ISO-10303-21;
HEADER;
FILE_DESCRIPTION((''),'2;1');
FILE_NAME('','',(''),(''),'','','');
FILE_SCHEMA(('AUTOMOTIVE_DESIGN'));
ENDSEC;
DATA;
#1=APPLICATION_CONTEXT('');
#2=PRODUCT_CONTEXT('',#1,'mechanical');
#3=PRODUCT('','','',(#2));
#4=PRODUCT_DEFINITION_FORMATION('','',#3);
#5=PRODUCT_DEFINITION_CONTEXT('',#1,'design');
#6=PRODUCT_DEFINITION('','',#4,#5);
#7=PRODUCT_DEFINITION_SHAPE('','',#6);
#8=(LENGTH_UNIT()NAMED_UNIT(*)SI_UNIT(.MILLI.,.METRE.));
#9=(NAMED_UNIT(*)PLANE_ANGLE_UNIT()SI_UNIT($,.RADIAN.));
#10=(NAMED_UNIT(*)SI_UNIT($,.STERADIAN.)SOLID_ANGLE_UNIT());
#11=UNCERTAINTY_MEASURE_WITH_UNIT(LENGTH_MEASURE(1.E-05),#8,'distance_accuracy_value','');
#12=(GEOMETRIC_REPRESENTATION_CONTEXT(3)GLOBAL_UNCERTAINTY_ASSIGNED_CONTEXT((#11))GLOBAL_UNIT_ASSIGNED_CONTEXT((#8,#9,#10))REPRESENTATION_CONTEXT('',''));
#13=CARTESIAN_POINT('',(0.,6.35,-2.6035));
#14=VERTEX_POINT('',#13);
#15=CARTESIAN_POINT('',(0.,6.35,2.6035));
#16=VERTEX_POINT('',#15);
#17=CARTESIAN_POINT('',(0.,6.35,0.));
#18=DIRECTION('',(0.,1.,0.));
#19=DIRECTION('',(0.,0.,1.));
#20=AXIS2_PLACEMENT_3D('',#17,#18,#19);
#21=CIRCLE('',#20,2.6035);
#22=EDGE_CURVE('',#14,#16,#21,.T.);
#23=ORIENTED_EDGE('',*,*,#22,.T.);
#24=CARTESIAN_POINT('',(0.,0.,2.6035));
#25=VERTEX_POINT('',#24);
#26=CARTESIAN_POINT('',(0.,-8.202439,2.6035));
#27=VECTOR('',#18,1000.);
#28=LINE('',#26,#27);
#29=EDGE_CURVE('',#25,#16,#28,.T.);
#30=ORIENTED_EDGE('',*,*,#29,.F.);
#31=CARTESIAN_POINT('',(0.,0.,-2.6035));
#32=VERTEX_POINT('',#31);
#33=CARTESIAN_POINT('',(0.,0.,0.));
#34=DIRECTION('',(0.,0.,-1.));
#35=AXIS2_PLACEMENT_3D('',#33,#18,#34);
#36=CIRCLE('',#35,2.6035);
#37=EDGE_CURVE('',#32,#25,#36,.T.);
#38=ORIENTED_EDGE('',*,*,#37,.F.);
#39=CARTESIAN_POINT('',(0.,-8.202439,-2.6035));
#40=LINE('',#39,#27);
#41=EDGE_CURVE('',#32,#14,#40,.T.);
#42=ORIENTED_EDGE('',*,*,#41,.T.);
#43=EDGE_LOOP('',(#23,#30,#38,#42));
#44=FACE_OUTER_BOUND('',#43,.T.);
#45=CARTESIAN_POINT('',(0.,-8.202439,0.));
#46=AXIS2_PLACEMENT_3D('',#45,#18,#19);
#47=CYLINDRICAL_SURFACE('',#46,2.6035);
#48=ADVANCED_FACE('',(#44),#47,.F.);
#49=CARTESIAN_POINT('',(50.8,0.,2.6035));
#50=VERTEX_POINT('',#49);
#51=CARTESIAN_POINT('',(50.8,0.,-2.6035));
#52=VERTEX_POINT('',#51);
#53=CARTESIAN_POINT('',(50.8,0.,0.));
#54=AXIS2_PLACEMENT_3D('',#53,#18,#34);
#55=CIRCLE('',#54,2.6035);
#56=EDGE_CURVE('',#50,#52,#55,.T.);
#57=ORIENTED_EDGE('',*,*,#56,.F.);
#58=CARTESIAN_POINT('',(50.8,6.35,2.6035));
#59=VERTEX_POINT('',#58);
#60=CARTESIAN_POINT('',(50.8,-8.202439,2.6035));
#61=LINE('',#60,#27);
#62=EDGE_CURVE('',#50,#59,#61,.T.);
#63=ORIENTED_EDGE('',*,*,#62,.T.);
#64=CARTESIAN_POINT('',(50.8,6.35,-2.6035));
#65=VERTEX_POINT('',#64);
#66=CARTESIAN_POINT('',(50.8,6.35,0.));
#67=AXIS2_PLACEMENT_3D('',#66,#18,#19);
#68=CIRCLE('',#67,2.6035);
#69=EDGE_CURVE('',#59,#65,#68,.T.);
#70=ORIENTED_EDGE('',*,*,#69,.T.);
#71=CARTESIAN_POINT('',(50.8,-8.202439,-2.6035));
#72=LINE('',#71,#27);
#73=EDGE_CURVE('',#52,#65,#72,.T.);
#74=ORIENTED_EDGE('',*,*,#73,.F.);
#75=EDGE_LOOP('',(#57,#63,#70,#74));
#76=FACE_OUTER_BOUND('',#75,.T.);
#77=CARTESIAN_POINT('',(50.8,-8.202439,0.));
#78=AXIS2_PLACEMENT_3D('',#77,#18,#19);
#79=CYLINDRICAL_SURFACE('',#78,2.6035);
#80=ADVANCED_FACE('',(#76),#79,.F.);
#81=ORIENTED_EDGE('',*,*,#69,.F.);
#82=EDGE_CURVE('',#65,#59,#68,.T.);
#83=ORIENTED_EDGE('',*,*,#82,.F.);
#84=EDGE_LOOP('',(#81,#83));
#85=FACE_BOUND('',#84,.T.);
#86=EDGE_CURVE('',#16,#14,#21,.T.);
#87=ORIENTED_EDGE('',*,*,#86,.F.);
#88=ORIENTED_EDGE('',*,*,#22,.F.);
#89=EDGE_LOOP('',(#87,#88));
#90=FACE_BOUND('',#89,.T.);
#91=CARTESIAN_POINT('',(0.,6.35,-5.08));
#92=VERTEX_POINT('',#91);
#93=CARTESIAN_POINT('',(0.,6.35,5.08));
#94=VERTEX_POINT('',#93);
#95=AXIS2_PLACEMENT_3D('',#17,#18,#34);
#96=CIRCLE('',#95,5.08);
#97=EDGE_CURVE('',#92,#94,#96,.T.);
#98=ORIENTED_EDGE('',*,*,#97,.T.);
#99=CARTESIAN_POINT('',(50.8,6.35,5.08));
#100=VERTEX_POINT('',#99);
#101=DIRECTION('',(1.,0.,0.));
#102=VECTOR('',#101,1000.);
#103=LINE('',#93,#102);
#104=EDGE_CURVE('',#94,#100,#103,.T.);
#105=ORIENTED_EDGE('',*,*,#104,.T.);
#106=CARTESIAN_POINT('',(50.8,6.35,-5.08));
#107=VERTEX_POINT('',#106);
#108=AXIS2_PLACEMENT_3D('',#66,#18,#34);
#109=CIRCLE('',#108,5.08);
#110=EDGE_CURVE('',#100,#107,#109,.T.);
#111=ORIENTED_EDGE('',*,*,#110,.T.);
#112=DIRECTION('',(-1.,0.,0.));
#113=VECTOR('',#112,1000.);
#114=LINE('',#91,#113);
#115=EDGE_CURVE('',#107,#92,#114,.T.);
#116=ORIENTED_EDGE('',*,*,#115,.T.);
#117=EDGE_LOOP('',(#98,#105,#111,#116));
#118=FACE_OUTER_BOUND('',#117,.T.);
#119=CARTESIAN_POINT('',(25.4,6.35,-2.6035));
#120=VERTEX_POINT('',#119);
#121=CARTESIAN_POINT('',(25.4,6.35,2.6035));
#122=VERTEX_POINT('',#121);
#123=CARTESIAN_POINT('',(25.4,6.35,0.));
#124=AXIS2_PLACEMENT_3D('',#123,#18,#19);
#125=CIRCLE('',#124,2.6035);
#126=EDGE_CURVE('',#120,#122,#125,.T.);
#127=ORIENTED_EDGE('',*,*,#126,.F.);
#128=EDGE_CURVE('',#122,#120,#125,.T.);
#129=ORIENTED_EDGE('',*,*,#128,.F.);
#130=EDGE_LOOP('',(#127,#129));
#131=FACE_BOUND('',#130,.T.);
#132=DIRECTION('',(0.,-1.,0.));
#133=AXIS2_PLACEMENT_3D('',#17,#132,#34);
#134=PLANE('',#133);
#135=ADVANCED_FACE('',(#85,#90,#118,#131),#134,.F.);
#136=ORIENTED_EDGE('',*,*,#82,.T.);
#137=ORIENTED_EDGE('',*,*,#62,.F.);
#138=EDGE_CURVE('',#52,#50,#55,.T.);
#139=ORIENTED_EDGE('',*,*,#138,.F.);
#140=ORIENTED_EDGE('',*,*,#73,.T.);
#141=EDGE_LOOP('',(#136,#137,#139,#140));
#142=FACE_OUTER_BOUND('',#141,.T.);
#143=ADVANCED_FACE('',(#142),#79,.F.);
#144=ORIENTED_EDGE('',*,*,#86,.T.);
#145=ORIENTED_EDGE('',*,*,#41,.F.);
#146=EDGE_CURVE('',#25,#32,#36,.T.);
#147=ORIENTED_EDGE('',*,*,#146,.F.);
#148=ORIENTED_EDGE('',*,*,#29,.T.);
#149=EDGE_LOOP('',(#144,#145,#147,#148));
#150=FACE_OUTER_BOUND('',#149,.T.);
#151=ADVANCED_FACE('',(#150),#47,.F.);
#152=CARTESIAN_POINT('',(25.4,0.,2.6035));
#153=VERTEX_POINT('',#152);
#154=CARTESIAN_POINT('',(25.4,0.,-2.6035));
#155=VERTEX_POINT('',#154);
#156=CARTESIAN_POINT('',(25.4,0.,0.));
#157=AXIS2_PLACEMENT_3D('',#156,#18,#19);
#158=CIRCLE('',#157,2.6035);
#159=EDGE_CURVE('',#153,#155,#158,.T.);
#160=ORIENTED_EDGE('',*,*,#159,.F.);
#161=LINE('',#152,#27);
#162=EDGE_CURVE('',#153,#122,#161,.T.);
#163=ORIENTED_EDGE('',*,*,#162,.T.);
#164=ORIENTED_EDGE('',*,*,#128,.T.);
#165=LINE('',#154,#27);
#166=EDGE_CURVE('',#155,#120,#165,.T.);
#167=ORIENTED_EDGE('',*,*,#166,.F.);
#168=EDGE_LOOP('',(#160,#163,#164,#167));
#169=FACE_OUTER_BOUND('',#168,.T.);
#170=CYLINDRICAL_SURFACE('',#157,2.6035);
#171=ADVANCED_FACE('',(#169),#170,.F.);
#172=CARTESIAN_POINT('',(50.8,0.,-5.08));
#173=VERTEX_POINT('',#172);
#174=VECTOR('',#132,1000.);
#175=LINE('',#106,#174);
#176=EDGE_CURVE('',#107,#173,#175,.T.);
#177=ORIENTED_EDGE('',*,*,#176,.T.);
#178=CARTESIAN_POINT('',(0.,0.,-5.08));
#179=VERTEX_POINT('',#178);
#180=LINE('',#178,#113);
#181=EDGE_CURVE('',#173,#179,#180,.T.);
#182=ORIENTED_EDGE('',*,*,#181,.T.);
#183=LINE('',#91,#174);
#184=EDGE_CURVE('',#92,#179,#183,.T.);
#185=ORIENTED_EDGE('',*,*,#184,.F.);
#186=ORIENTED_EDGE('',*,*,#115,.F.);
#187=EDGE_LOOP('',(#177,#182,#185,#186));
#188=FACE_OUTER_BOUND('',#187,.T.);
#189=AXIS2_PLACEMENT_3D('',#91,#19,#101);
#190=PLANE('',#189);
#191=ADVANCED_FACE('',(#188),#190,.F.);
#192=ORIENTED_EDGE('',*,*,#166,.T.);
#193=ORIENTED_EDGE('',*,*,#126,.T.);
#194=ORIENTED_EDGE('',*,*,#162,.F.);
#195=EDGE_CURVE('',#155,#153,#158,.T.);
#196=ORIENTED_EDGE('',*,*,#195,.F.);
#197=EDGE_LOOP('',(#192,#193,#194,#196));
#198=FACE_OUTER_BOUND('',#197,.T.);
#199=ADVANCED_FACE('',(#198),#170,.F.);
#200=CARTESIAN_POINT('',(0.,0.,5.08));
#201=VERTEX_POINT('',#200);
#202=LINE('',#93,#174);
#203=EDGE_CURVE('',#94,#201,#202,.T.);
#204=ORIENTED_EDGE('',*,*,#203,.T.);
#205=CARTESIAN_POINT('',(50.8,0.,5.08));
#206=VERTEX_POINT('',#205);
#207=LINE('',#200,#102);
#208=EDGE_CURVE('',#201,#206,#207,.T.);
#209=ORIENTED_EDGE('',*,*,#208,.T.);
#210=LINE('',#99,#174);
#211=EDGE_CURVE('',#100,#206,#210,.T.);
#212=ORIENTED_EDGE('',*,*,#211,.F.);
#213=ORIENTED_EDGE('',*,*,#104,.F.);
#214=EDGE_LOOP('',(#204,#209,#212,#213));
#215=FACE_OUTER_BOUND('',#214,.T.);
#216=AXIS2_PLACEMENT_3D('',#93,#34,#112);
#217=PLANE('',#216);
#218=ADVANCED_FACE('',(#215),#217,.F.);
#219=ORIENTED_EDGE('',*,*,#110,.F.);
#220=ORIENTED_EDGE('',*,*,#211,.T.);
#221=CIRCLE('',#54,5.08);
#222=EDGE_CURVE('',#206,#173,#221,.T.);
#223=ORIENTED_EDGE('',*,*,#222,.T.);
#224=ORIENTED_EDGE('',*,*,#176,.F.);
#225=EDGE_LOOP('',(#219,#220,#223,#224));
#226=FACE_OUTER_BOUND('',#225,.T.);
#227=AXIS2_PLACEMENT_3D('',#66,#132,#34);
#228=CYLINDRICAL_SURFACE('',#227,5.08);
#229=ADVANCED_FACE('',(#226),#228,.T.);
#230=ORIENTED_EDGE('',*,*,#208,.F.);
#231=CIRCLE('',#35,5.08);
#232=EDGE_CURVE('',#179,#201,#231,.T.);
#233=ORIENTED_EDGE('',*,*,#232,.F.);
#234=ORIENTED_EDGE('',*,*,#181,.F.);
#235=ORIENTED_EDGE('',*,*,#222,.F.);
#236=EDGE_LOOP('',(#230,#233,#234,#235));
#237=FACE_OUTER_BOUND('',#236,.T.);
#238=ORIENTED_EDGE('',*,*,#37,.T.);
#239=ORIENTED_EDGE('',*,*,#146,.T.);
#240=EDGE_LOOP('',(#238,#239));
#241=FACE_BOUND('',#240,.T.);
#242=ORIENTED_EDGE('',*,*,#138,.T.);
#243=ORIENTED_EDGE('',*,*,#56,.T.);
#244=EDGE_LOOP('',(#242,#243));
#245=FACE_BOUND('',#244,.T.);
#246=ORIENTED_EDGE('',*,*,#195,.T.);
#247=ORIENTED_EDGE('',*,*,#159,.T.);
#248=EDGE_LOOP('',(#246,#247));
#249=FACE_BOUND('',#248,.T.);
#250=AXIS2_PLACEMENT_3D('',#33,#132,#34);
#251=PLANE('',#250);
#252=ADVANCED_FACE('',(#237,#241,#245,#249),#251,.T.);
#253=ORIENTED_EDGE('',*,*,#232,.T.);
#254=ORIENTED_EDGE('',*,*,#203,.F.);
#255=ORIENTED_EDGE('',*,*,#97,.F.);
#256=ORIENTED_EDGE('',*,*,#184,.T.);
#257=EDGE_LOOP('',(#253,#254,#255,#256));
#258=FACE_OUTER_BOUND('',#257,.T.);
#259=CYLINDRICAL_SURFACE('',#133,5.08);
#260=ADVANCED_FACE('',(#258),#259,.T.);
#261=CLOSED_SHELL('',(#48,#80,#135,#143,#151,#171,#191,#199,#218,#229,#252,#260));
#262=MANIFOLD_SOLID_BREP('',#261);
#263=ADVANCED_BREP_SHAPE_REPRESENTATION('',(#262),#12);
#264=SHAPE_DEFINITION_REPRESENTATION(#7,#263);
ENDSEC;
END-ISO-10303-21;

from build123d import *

# Parameters (mm, degrees)
SKETCH1_R           = 2.9
BOSS_EXTRUDE1_DEPTH = 6.35
BOSS_EXTRUDE2_START = -6.35
SKETCH2_R           = 2.9
SKETCH2_R_2         = 2.6035
BOSS_EXTRUDE2_DEPTH = 6.35
SKETCH2_2_R         = 2.6035
CUT_EXTRUDE1_DEPTH  = 57.468604552


with BuildPart() as part:
    # Sketch1 → Boss-Extrude1 (new body)
    with BuildSketch(Plane(origin=(0, 0, 0), x_dir=(1, 0, 0), z_dir=(0, 1, 0))):
        with BuildLine():
            Line((0, 5.08), (50.8, 5.08))
            ThreePointArc((50.8, 5.08), (55.88, 0), (50.8, -5.08))
            Line((50.8, -5.08), (0, -5.08))
            ThreePointArc((0, -5.08), (-5.08, 0), (0, 5.08))
        make_face()
        with Locations(Location((0, 0, 0), (0, 0, 270))):
            Circle(SKETCH1_R, mode=Mode.SUBTRACT)
        with Locations(Location((50.8, 0, 0), (0, 0, 270))):
            Circle(SKETCH1_R, mode=Mode.SUBTRACT)
    extrude(amount=BOSS_EXTRUDE1_DEPTH)

    # Sketch2 → Boss-Extrude2 (add)
    # profile 1 of 3: a face of its own
    with BuildSketch(Plane(origin=(0, 6.35, 0), x_dir=(1, 0, 0), z_dir=(0, 1, 0)).offset(BOSS_EXTRUDE2_START)):
        Circle(SKETCH2_R)
        with Locations(Location((0, 0, 0), (0, 0, 270))):
            Circle(SKETCH2_R_2, mode=Mode.SUBTRACT)
    # profile 2 of 3: a face of its own
    with BuildSketch(Plane(origin=(0, 6.35, 0), x_dir=(1, 0, 0), z_dir=(0, 1, 0)).offset(BOSS_EXTRUDE2_START)):
        with Locations((50.8, 0)):
            Circle(SKETCH2_R)
        with Locations(Location((50.8, 0, 0), (0, 0, 270))):
            Circle(SKETCH2_R_2, mode=Mode.SUBTRACT)
    # profile 3 of 3: a face of its own
    with BuildSketch(Plane(origin=(0, 6.35, 0), x_dir=(1, 0, 0), z_dir=(0, 1, 0)).offset(BOSS_EXTRUDE2_START)):
        with Locations((25.4, 0)):
            Circle(SKETCH2_R_2)
    extrude(amount=BOSS_EXTRUDE2_DEPTH)

    # Sketch2<2> → Cut-Extrude1 (cut, through all)
    with BuildSketch(Plane(origin=(0, 6.35, 0), x_dir=(1, 0, 0), z_dir=(0, 1, 0))):
        with Locations(Location((25.4, 0, 0), (0, 0, 270))):
            Circle(SKETCH2_2_R)
    extrude(amount=-CUT_EXTRUDE1_DEPTH, mode=Mode.SUBTRACT)


solid = part.part
